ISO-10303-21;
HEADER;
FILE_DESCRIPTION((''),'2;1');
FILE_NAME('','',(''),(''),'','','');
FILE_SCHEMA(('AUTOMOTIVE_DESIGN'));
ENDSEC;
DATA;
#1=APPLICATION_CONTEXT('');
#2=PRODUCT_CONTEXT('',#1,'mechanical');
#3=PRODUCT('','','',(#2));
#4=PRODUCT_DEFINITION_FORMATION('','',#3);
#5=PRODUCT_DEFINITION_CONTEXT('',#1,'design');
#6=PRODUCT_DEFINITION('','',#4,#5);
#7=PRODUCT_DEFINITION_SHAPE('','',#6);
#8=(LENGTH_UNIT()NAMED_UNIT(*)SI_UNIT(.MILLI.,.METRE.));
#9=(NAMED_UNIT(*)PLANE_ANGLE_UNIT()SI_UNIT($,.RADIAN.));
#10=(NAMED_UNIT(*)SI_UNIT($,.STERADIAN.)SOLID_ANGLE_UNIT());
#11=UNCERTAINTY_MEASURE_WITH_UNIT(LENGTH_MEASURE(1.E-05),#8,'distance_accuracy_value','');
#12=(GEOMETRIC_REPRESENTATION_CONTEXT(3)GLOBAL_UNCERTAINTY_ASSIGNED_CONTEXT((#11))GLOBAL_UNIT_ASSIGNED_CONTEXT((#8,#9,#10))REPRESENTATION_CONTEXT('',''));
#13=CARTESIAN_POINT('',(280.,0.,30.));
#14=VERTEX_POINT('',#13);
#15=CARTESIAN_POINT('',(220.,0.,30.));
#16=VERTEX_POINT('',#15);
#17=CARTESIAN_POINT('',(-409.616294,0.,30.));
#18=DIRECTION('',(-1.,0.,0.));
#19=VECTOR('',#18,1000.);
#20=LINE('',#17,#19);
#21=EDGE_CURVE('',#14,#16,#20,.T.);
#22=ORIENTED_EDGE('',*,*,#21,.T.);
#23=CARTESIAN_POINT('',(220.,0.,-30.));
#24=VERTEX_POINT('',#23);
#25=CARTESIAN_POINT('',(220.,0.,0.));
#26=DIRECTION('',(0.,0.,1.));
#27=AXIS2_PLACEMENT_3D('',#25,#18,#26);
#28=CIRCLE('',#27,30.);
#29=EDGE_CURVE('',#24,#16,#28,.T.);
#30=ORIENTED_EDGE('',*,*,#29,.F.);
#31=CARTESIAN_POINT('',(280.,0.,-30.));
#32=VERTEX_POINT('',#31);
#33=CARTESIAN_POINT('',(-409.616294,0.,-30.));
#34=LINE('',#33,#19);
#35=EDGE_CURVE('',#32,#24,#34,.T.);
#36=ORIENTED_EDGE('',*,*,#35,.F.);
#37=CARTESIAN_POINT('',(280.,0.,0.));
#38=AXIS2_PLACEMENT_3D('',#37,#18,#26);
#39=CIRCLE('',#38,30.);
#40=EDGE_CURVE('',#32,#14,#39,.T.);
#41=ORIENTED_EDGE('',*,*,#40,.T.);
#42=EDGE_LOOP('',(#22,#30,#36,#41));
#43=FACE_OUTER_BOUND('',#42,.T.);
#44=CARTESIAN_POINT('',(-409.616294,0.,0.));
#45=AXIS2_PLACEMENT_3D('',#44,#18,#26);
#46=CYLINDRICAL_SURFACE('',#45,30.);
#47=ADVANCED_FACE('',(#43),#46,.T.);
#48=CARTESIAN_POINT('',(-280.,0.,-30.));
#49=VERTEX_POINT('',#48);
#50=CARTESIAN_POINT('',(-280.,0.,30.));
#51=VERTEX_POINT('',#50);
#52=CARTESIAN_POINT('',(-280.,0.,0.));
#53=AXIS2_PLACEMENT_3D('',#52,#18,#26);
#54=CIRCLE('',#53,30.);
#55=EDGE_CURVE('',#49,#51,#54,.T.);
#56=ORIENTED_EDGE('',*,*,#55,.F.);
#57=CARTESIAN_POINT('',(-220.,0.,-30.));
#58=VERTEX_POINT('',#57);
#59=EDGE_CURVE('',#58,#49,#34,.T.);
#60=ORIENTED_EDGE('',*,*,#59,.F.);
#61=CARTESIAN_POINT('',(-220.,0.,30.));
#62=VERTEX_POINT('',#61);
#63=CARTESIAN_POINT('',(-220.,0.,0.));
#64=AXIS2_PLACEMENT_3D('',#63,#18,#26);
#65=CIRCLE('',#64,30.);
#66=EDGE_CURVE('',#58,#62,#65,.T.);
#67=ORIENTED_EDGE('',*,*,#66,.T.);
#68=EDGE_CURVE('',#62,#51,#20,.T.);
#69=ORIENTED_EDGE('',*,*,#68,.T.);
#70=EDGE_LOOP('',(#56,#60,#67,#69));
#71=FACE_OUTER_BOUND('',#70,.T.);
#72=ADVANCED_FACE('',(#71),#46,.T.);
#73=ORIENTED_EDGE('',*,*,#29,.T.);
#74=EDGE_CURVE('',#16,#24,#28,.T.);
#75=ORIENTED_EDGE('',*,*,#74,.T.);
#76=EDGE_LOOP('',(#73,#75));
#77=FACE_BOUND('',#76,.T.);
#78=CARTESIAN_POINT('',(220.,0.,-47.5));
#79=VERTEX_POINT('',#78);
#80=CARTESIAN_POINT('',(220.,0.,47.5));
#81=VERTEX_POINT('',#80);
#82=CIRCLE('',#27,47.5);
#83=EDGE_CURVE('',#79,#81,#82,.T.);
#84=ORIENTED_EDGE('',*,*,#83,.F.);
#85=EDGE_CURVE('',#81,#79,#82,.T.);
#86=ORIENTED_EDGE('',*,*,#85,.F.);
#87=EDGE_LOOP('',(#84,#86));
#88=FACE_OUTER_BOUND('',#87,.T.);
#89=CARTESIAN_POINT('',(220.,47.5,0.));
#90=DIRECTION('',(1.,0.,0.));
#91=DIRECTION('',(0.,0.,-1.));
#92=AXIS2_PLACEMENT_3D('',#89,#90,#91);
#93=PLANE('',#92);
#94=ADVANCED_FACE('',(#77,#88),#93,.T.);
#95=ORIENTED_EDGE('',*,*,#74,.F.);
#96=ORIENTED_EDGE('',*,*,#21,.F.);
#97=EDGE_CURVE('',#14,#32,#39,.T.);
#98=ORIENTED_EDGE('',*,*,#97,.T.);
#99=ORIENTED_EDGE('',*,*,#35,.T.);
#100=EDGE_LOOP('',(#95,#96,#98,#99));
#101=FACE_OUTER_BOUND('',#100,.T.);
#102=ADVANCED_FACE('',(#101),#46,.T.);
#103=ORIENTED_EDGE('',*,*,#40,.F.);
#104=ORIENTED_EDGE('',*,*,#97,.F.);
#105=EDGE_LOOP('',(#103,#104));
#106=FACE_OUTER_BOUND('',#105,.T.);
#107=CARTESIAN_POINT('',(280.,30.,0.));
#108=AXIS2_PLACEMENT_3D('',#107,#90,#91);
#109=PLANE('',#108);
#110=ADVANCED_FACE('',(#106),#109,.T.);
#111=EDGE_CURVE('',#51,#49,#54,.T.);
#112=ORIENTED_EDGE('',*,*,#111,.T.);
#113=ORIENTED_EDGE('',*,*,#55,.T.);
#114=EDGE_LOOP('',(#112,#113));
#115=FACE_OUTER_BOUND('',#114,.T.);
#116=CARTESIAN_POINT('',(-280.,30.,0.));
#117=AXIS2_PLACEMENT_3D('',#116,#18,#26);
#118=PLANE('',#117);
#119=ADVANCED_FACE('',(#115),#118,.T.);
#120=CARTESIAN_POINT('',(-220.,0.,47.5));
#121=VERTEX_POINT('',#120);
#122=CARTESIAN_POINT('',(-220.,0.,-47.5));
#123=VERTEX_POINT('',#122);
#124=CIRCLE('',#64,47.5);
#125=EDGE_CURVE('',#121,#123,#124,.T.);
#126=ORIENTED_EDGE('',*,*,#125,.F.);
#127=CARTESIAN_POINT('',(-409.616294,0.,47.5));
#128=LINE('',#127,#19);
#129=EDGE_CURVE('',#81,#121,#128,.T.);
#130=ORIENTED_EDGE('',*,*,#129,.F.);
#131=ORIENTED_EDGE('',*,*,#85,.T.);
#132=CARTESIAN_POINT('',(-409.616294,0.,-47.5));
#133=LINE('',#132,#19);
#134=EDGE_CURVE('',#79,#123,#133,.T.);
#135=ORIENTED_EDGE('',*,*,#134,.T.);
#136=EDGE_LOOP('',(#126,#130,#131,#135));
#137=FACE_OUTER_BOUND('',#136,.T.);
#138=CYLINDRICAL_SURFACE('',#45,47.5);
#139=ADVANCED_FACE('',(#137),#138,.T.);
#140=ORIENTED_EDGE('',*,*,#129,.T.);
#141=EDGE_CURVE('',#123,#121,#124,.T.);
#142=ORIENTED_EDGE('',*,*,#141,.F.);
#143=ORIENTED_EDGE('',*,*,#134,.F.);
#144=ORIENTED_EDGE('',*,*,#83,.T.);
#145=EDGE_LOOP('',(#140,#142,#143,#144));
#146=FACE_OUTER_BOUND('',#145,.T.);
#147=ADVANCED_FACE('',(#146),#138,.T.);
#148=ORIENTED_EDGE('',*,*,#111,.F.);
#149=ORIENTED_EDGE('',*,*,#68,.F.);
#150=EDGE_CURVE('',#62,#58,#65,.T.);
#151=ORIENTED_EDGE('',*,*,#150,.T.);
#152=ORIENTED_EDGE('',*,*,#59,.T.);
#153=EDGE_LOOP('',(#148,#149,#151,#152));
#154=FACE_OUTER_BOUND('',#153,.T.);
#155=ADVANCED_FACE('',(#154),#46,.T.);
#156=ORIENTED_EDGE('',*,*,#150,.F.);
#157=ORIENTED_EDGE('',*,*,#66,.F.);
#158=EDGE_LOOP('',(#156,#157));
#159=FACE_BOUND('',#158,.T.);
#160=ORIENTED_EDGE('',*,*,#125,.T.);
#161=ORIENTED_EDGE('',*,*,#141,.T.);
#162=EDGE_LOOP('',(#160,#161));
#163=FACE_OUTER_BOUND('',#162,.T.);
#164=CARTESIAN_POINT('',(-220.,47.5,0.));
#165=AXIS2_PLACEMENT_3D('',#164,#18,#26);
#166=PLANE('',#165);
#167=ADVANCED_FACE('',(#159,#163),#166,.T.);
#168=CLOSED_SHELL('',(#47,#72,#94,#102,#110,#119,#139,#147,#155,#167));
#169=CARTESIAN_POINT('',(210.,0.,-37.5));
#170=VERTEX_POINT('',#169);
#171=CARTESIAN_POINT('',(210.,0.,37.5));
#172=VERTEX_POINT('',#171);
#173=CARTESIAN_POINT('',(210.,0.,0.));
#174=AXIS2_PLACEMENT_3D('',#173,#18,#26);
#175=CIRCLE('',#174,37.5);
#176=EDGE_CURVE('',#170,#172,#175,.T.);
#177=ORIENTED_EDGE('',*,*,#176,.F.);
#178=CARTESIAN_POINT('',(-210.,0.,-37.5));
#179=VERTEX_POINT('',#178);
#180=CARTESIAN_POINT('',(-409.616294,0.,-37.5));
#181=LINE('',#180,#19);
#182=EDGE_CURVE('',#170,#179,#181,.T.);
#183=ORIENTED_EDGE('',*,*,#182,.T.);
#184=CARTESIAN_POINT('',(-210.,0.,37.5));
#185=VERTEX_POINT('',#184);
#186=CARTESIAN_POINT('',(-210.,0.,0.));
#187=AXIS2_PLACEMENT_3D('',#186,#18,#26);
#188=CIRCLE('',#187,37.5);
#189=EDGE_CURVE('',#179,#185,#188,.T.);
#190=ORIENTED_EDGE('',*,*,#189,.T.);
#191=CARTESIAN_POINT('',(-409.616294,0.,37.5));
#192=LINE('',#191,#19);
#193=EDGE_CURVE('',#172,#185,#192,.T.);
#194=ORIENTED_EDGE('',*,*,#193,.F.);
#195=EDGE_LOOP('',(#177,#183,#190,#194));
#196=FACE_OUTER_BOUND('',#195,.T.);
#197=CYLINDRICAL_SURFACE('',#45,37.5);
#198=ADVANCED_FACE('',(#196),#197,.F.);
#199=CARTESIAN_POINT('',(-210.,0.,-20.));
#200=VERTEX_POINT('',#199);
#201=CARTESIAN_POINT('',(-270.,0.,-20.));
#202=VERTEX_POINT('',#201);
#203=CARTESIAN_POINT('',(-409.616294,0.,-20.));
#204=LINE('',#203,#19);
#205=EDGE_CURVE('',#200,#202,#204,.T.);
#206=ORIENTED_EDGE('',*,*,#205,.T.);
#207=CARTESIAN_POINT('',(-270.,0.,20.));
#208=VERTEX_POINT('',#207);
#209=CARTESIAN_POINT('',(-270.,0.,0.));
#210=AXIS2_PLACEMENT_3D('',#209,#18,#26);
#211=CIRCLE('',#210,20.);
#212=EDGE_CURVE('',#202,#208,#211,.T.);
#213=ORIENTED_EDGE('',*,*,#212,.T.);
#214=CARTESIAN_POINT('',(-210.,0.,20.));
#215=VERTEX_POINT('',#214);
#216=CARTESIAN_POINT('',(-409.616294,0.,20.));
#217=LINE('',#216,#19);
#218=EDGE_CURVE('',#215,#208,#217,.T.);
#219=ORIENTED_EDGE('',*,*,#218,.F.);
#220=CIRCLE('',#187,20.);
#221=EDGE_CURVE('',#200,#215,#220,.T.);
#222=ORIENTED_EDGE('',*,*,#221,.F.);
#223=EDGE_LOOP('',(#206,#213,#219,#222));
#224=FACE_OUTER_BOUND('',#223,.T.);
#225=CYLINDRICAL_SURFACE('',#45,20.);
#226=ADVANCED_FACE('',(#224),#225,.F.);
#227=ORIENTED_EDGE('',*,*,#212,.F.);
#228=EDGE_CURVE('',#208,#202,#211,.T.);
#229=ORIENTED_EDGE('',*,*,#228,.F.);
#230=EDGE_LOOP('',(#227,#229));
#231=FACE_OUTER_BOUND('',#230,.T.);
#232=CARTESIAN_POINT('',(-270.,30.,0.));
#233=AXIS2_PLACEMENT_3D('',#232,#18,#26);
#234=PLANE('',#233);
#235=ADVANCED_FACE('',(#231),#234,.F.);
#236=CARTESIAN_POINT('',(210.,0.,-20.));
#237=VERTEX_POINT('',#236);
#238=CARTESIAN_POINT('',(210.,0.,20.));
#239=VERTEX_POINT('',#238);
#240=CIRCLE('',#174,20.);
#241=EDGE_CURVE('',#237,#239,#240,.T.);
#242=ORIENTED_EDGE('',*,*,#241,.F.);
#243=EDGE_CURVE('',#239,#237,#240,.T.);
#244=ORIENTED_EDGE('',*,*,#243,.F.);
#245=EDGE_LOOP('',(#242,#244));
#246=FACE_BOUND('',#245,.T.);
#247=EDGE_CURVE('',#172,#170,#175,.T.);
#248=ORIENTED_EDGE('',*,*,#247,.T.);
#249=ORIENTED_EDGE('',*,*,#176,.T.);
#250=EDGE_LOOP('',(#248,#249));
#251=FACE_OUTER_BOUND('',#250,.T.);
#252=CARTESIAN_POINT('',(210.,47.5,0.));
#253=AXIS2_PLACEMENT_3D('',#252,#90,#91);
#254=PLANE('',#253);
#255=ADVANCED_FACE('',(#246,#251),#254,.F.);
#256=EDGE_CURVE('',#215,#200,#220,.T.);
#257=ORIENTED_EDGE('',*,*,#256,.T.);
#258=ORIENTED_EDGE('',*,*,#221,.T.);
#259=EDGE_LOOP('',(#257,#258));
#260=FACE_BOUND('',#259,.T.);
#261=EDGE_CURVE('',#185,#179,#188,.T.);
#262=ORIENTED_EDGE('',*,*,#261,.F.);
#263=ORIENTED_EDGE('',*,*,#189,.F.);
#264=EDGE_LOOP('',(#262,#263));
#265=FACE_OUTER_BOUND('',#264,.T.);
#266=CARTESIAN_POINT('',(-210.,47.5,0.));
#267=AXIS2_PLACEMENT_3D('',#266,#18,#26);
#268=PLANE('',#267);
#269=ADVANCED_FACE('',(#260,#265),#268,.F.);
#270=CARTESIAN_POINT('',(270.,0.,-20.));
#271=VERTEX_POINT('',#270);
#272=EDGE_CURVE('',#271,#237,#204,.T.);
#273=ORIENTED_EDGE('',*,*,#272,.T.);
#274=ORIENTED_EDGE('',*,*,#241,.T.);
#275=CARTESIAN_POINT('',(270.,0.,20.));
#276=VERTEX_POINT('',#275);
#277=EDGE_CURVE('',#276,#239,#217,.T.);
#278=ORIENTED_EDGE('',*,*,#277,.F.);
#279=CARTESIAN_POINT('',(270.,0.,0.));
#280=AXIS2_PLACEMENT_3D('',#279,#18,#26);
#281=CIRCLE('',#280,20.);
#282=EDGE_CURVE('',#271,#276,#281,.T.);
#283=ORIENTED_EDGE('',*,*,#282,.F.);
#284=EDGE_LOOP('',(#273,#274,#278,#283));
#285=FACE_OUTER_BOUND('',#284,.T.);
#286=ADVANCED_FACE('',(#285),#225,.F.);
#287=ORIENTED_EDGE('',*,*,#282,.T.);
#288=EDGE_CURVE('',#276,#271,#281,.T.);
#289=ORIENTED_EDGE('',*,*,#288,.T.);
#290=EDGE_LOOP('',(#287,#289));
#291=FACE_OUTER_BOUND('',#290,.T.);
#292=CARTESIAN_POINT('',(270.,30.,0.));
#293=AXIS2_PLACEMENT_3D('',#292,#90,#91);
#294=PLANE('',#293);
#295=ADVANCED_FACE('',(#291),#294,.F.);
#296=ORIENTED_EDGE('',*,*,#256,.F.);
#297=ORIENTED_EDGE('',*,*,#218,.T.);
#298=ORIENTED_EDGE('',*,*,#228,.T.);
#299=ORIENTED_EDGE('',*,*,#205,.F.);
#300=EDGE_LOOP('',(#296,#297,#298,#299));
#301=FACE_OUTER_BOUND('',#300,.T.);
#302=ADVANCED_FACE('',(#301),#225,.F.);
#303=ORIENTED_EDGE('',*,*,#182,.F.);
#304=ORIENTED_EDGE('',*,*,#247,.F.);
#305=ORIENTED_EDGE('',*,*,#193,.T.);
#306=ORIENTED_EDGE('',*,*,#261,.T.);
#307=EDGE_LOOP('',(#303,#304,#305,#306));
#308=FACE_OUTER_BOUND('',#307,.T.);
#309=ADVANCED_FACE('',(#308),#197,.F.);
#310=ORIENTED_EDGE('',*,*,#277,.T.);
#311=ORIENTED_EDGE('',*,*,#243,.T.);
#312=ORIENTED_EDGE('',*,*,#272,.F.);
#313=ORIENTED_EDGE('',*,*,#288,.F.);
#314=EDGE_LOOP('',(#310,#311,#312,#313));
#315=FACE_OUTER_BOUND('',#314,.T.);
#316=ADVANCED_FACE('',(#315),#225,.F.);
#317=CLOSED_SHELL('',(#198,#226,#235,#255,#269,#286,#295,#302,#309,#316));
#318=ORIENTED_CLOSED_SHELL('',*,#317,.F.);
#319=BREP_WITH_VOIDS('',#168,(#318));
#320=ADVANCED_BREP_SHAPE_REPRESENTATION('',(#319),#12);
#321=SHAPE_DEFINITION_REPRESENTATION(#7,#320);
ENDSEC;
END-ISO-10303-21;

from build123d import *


with BuildPart() as part:
    # Roller Profile Sketch → Roller Body Thin Revolve (revolve)
    with BuildSketch(Plane.XY, mode=Mode.PRIVATE) as roller_body_thin_revolve_sk:
        Polygon((280, 0), (280, 30), (220, 30), (220, 47.5), (-220, 47.5), (-220, 30), (-280, 30), (-280, 0), (-270, 0), (-270, 20), (-210, 20), (-210, 37.5), (210, 37.5), (210, 20), (270, 20), (270, 0), align=None)
    revolve(roller_body_thin_revolve_sk.sketch.rotate(Axis((-409.616293783, 0, 0), (1, 0, 0)), 90), axis=Axis((-409.616293783, 0, 0), (1, 0, 0)))


solid = part.part
